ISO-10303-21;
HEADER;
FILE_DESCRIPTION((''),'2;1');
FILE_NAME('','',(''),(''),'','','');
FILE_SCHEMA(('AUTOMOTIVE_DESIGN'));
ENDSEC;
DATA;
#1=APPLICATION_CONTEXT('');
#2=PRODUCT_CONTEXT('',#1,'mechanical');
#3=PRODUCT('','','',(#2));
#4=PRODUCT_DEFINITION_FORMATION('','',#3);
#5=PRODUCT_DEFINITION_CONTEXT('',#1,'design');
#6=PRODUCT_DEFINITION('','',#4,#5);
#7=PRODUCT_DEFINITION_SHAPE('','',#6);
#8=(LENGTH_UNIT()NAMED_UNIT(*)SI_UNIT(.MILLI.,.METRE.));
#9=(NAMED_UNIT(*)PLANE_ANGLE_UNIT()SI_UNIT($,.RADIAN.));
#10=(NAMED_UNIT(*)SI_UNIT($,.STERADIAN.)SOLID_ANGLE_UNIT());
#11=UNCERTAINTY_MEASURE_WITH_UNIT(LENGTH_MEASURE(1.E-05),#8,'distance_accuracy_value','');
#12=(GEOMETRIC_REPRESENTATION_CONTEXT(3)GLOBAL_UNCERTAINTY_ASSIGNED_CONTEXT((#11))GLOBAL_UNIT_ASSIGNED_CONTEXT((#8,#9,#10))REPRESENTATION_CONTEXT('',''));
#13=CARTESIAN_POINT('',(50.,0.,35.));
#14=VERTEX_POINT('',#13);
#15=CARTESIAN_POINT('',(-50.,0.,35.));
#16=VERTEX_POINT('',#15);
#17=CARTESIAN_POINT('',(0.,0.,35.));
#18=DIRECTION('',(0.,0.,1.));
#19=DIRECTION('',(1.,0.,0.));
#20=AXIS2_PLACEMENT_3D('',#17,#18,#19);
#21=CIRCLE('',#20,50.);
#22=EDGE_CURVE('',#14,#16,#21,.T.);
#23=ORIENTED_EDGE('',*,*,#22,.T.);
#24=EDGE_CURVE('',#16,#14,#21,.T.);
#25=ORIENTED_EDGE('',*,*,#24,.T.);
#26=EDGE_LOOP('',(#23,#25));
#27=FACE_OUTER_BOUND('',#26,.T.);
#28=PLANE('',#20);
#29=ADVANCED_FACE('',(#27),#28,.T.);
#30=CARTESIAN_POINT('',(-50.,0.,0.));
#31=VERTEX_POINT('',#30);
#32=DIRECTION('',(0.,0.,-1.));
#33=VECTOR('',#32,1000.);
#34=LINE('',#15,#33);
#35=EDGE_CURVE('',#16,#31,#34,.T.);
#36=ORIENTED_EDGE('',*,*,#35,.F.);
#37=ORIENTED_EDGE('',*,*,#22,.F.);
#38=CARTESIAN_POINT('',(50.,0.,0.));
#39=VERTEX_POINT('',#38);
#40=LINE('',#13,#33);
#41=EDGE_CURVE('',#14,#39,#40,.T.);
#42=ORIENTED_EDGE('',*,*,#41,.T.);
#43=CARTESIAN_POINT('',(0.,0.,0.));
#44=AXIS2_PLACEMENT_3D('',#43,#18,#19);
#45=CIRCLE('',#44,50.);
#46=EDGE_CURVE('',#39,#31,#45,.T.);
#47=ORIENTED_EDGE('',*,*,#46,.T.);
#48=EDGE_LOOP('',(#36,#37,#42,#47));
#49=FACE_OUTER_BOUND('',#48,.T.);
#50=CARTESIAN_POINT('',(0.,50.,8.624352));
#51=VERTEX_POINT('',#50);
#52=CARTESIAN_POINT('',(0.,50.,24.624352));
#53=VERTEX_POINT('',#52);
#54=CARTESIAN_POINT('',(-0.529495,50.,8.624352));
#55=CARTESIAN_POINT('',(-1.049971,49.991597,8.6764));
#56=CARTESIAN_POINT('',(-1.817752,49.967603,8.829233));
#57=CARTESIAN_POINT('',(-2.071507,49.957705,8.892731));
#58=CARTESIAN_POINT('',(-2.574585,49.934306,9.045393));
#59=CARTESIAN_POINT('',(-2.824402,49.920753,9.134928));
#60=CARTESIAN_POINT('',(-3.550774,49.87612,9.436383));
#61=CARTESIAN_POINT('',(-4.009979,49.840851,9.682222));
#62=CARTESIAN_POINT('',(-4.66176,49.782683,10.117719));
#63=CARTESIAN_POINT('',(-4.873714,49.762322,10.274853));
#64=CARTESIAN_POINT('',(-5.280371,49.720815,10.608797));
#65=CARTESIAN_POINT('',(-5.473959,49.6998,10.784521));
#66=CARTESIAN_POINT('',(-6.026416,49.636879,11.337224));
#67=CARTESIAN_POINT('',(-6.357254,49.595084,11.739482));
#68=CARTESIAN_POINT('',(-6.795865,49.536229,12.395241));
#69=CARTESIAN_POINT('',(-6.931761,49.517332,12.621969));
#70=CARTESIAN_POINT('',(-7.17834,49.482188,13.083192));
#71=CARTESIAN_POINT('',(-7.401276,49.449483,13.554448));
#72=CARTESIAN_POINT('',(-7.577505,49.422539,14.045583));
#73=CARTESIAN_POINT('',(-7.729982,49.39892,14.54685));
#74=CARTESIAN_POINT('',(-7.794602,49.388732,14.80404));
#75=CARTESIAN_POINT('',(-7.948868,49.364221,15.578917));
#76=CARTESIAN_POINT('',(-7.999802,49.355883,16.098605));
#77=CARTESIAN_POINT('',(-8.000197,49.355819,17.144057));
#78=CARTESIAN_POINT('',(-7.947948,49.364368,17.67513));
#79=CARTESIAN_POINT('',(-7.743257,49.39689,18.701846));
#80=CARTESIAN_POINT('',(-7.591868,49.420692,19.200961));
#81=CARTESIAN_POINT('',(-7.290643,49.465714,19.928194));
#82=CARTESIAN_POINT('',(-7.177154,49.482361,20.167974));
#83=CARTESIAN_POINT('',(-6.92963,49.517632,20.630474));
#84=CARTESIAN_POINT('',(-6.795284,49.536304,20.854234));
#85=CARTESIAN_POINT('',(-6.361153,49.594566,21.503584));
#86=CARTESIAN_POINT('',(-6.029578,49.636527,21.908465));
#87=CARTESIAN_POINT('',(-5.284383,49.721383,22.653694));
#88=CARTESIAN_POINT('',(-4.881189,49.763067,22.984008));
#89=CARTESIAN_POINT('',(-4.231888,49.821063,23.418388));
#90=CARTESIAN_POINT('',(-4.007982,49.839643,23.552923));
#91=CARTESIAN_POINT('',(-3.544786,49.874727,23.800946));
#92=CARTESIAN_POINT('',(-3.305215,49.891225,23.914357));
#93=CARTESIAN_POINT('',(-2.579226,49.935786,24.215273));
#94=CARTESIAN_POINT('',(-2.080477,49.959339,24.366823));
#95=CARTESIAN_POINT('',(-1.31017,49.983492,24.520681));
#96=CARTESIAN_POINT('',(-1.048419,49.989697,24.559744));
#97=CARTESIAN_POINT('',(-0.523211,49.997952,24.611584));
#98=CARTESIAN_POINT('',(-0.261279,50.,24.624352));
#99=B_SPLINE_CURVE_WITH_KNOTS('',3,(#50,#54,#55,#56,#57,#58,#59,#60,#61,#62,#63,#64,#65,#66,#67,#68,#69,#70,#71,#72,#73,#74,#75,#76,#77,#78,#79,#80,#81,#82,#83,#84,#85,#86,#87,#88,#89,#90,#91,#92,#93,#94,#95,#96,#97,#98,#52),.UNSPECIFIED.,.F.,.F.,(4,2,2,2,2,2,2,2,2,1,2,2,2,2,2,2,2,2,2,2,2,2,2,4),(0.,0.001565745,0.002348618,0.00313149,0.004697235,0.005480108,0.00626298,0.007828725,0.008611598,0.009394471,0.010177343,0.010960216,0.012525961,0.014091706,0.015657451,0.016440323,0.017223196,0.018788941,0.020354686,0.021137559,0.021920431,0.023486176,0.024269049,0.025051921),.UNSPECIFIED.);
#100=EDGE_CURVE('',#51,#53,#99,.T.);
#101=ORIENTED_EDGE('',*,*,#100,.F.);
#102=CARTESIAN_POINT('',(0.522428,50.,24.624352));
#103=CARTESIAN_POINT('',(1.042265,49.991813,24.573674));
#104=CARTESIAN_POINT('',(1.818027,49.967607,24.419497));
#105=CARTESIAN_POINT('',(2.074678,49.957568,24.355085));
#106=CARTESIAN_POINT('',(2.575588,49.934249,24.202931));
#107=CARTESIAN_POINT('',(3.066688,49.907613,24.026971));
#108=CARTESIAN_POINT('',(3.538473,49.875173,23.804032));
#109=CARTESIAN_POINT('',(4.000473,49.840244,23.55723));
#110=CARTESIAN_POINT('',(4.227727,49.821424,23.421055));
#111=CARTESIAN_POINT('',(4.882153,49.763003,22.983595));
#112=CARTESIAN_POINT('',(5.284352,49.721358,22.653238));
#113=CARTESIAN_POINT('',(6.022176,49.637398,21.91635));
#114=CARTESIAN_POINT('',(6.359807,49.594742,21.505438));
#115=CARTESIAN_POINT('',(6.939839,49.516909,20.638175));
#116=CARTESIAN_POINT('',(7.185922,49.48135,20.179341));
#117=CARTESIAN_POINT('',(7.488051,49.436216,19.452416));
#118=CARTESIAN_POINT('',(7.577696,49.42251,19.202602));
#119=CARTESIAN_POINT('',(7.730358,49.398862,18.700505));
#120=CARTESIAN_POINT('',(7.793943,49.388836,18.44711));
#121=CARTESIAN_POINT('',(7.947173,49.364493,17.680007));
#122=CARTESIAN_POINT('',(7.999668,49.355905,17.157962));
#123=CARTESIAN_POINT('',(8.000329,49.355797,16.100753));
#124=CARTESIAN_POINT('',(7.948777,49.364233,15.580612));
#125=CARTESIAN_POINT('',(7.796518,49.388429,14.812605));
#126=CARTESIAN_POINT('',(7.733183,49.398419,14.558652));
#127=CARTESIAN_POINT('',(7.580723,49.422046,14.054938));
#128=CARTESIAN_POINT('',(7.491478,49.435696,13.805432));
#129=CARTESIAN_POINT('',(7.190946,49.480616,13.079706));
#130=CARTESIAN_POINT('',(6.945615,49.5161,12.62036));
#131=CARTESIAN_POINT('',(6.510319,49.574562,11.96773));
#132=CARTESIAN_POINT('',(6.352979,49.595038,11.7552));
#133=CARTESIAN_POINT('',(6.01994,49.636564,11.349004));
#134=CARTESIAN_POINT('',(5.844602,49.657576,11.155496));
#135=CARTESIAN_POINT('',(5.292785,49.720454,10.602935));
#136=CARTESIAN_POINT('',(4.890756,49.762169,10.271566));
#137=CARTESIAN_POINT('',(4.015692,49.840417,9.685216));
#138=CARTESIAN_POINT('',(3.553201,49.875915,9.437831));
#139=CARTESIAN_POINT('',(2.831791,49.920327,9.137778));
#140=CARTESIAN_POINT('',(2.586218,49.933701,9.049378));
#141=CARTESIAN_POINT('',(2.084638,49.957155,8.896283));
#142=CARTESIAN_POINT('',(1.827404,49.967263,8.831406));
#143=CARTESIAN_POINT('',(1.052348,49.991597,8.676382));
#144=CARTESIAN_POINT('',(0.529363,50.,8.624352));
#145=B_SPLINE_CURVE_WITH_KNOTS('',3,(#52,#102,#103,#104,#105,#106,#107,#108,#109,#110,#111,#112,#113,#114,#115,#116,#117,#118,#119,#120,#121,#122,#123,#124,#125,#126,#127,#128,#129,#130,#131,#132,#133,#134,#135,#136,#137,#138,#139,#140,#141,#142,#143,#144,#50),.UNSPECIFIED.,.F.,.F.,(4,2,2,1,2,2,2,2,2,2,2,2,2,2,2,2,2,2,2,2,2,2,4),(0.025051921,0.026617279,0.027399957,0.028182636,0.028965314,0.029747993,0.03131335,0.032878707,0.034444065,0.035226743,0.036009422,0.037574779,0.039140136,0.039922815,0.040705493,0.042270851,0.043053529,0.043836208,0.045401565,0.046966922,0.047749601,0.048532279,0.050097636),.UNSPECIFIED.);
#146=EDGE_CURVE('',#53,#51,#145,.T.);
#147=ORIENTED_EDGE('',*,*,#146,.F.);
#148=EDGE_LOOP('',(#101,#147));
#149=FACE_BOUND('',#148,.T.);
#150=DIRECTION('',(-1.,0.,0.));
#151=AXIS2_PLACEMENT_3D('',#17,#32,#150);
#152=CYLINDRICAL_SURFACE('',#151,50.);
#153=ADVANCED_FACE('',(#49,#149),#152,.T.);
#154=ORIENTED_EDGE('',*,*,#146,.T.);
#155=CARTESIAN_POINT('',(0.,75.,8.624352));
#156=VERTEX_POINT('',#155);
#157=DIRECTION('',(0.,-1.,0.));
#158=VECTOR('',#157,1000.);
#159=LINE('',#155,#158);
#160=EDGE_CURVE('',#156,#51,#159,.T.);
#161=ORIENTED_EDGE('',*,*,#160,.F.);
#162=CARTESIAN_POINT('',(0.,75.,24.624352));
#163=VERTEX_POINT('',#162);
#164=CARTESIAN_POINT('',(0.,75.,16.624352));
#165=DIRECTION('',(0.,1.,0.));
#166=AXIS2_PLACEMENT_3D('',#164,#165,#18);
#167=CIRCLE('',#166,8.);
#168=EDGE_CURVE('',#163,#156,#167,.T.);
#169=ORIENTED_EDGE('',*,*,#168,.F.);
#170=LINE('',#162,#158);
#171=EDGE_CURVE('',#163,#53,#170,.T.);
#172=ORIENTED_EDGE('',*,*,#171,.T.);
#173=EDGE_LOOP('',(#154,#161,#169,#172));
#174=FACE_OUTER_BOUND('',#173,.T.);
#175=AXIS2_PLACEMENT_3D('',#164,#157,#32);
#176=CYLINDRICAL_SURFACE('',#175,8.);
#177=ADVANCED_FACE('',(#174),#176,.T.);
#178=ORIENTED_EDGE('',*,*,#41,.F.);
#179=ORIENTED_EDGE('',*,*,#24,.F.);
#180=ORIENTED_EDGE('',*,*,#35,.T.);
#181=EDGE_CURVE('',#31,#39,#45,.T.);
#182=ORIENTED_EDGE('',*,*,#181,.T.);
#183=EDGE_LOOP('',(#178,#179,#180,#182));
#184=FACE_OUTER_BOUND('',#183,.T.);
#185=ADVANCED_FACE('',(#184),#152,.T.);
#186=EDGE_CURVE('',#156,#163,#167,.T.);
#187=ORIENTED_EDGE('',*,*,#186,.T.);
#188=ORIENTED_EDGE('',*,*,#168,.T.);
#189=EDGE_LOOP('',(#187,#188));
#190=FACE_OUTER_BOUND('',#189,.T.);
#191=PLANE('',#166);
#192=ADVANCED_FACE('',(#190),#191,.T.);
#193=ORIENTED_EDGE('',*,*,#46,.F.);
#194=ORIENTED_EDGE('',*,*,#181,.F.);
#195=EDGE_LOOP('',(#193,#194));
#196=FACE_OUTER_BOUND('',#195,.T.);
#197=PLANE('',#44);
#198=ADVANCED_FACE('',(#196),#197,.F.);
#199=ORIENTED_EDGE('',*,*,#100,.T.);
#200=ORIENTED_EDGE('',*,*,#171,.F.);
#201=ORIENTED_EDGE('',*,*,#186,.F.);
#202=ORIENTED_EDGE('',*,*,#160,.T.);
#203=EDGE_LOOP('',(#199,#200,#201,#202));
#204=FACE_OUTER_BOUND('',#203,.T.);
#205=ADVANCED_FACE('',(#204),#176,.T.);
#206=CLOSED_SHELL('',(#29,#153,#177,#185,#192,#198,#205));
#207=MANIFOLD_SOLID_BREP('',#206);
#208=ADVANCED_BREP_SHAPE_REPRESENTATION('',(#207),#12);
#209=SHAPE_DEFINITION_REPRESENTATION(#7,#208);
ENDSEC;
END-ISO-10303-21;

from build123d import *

# Parameters (mm, degrees)
SKETCH1_R           = 50
BOSS_EXTRUDE1_DEPTH = 35
SKETCH2_R           = 8
BOSS_EXTRUDE2_DEPTH = 75


with BuildPart() as part:
    # Sketch1 → Boss-Extrude1 (new body)
    with BuildSketch(Plane.XY):
        Circle(SKETCH1_R)
    extrude(amount=BOSS_EXTRUDE1_DEPTH)

    # Sketch2 → Boss-Extrude2 (add)
    with BuildSketch(Plane(origin=(0, 0, 0), x_dir=(1, 0, 0), z_dir=(0, 1, 0))):
        with Locations(Location((0, -16.62435188, 0), (0, 0, 90))):
            Circle(SKETCH2_R)
    extrude(amount=BOSS_EXTRUDE2_DEPTH)


solid = part.part
